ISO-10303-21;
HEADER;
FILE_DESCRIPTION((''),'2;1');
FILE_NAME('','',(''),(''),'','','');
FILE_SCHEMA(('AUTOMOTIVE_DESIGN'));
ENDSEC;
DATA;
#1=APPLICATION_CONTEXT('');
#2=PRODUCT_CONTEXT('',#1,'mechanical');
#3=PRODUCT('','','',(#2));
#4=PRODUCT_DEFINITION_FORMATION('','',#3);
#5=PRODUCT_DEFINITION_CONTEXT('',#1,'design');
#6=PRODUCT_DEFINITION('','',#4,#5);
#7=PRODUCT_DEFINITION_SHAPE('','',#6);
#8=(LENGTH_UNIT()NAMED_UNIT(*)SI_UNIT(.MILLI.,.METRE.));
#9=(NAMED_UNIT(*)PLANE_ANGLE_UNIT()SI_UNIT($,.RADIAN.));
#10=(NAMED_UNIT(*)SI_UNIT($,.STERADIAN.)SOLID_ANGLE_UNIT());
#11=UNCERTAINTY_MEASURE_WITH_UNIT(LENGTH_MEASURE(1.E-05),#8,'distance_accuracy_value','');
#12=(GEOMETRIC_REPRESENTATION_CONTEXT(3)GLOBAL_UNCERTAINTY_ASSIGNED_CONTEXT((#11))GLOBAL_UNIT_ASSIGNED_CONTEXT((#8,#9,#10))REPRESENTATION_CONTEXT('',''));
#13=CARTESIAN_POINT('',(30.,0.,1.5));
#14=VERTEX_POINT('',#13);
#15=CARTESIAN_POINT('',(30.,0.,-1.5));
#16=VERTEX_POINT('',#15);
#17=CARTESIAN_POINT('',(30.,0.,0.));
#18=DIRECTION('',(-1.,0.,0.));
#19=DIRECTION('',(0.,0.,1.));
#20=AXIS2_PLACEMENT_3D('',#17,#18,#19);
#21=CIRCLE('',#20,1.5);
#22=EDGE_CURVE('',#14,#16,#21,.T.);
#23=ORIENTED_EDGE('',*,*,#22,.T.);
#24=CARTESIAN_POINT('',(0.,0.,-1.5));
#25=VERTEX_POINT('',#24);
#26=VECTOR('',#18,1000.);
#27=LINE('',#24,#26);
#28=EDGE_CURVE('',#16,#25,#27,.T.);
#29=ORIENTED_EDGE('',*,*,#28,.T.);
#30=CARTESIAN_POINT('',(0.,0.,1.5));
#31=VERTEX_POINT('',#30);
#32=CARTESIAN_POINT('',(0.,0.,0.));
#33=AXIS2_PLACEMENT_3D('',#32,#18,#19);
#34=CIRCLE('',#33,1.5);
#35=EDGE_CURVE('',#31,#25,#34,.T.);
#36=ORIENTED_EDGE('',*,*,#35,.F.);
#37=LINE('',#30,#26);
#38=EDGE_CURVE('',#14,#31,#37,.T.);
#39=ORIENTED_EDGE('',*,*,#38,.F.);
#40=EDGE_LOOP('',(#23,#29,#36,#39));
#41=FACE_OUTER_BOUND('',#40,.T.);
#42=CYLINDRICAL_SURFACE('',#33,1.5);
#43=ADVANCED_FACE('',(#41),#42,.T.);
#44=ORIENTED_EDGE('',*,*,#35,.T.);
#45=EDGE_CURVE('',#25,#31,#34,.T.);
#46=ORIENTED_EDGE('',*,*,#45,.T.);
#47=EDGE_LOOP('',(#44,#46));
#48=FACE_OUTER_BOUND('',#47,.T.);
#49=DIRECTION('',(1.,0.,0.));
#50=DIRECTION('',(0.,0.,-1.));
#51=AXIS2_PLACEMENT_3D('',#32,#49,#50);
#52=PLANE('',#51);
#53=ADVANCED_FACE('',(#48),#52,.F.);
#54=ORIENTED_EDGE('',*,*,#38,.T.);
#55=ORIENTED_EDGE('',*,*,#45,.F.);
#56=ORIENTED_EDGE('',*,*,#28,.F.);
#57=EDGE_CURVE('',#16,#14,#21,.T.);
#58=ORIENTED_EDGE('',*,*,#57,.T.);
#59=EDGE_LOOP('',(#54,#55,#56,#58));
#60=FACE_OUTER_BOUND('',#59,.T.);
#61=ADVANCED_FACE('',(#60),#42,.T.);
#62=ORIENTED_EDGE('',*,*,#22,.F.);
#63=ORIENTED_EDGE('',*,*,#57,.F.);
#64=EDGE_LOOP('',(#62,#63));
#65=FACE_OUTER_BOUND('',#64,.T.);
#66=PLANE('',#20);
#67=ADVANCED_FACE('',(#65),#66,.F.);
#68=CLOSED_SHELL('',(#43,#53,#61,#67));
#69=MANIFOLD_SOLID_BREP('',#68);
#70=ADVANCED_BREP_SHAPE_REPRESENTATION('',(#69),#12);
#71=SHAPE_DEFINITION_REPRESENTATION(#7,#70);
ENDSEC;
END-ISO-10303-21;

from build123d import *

# Parameters (mm, degrees)
SKETCH1_W = 30
SKETCH1_H = 1.5


with BuildPart() as part:
    # Sketch1 → Revolve1 (revolve)
    with BuildSketch(Plane.XY, mode=Mode.PRIVATE) as revolve1_sk:
        with Locations((15, 0.75)):
            Rectangle(SKETCH1_W, SKETCH1_H)
    revolve(revolve1_sk.sketch.rotate(Axis((0, 0, 0), (1, 0, 0)), 90), axis=Axis((0, 0, 0), (1, 0, 0)))


solid = part.part
